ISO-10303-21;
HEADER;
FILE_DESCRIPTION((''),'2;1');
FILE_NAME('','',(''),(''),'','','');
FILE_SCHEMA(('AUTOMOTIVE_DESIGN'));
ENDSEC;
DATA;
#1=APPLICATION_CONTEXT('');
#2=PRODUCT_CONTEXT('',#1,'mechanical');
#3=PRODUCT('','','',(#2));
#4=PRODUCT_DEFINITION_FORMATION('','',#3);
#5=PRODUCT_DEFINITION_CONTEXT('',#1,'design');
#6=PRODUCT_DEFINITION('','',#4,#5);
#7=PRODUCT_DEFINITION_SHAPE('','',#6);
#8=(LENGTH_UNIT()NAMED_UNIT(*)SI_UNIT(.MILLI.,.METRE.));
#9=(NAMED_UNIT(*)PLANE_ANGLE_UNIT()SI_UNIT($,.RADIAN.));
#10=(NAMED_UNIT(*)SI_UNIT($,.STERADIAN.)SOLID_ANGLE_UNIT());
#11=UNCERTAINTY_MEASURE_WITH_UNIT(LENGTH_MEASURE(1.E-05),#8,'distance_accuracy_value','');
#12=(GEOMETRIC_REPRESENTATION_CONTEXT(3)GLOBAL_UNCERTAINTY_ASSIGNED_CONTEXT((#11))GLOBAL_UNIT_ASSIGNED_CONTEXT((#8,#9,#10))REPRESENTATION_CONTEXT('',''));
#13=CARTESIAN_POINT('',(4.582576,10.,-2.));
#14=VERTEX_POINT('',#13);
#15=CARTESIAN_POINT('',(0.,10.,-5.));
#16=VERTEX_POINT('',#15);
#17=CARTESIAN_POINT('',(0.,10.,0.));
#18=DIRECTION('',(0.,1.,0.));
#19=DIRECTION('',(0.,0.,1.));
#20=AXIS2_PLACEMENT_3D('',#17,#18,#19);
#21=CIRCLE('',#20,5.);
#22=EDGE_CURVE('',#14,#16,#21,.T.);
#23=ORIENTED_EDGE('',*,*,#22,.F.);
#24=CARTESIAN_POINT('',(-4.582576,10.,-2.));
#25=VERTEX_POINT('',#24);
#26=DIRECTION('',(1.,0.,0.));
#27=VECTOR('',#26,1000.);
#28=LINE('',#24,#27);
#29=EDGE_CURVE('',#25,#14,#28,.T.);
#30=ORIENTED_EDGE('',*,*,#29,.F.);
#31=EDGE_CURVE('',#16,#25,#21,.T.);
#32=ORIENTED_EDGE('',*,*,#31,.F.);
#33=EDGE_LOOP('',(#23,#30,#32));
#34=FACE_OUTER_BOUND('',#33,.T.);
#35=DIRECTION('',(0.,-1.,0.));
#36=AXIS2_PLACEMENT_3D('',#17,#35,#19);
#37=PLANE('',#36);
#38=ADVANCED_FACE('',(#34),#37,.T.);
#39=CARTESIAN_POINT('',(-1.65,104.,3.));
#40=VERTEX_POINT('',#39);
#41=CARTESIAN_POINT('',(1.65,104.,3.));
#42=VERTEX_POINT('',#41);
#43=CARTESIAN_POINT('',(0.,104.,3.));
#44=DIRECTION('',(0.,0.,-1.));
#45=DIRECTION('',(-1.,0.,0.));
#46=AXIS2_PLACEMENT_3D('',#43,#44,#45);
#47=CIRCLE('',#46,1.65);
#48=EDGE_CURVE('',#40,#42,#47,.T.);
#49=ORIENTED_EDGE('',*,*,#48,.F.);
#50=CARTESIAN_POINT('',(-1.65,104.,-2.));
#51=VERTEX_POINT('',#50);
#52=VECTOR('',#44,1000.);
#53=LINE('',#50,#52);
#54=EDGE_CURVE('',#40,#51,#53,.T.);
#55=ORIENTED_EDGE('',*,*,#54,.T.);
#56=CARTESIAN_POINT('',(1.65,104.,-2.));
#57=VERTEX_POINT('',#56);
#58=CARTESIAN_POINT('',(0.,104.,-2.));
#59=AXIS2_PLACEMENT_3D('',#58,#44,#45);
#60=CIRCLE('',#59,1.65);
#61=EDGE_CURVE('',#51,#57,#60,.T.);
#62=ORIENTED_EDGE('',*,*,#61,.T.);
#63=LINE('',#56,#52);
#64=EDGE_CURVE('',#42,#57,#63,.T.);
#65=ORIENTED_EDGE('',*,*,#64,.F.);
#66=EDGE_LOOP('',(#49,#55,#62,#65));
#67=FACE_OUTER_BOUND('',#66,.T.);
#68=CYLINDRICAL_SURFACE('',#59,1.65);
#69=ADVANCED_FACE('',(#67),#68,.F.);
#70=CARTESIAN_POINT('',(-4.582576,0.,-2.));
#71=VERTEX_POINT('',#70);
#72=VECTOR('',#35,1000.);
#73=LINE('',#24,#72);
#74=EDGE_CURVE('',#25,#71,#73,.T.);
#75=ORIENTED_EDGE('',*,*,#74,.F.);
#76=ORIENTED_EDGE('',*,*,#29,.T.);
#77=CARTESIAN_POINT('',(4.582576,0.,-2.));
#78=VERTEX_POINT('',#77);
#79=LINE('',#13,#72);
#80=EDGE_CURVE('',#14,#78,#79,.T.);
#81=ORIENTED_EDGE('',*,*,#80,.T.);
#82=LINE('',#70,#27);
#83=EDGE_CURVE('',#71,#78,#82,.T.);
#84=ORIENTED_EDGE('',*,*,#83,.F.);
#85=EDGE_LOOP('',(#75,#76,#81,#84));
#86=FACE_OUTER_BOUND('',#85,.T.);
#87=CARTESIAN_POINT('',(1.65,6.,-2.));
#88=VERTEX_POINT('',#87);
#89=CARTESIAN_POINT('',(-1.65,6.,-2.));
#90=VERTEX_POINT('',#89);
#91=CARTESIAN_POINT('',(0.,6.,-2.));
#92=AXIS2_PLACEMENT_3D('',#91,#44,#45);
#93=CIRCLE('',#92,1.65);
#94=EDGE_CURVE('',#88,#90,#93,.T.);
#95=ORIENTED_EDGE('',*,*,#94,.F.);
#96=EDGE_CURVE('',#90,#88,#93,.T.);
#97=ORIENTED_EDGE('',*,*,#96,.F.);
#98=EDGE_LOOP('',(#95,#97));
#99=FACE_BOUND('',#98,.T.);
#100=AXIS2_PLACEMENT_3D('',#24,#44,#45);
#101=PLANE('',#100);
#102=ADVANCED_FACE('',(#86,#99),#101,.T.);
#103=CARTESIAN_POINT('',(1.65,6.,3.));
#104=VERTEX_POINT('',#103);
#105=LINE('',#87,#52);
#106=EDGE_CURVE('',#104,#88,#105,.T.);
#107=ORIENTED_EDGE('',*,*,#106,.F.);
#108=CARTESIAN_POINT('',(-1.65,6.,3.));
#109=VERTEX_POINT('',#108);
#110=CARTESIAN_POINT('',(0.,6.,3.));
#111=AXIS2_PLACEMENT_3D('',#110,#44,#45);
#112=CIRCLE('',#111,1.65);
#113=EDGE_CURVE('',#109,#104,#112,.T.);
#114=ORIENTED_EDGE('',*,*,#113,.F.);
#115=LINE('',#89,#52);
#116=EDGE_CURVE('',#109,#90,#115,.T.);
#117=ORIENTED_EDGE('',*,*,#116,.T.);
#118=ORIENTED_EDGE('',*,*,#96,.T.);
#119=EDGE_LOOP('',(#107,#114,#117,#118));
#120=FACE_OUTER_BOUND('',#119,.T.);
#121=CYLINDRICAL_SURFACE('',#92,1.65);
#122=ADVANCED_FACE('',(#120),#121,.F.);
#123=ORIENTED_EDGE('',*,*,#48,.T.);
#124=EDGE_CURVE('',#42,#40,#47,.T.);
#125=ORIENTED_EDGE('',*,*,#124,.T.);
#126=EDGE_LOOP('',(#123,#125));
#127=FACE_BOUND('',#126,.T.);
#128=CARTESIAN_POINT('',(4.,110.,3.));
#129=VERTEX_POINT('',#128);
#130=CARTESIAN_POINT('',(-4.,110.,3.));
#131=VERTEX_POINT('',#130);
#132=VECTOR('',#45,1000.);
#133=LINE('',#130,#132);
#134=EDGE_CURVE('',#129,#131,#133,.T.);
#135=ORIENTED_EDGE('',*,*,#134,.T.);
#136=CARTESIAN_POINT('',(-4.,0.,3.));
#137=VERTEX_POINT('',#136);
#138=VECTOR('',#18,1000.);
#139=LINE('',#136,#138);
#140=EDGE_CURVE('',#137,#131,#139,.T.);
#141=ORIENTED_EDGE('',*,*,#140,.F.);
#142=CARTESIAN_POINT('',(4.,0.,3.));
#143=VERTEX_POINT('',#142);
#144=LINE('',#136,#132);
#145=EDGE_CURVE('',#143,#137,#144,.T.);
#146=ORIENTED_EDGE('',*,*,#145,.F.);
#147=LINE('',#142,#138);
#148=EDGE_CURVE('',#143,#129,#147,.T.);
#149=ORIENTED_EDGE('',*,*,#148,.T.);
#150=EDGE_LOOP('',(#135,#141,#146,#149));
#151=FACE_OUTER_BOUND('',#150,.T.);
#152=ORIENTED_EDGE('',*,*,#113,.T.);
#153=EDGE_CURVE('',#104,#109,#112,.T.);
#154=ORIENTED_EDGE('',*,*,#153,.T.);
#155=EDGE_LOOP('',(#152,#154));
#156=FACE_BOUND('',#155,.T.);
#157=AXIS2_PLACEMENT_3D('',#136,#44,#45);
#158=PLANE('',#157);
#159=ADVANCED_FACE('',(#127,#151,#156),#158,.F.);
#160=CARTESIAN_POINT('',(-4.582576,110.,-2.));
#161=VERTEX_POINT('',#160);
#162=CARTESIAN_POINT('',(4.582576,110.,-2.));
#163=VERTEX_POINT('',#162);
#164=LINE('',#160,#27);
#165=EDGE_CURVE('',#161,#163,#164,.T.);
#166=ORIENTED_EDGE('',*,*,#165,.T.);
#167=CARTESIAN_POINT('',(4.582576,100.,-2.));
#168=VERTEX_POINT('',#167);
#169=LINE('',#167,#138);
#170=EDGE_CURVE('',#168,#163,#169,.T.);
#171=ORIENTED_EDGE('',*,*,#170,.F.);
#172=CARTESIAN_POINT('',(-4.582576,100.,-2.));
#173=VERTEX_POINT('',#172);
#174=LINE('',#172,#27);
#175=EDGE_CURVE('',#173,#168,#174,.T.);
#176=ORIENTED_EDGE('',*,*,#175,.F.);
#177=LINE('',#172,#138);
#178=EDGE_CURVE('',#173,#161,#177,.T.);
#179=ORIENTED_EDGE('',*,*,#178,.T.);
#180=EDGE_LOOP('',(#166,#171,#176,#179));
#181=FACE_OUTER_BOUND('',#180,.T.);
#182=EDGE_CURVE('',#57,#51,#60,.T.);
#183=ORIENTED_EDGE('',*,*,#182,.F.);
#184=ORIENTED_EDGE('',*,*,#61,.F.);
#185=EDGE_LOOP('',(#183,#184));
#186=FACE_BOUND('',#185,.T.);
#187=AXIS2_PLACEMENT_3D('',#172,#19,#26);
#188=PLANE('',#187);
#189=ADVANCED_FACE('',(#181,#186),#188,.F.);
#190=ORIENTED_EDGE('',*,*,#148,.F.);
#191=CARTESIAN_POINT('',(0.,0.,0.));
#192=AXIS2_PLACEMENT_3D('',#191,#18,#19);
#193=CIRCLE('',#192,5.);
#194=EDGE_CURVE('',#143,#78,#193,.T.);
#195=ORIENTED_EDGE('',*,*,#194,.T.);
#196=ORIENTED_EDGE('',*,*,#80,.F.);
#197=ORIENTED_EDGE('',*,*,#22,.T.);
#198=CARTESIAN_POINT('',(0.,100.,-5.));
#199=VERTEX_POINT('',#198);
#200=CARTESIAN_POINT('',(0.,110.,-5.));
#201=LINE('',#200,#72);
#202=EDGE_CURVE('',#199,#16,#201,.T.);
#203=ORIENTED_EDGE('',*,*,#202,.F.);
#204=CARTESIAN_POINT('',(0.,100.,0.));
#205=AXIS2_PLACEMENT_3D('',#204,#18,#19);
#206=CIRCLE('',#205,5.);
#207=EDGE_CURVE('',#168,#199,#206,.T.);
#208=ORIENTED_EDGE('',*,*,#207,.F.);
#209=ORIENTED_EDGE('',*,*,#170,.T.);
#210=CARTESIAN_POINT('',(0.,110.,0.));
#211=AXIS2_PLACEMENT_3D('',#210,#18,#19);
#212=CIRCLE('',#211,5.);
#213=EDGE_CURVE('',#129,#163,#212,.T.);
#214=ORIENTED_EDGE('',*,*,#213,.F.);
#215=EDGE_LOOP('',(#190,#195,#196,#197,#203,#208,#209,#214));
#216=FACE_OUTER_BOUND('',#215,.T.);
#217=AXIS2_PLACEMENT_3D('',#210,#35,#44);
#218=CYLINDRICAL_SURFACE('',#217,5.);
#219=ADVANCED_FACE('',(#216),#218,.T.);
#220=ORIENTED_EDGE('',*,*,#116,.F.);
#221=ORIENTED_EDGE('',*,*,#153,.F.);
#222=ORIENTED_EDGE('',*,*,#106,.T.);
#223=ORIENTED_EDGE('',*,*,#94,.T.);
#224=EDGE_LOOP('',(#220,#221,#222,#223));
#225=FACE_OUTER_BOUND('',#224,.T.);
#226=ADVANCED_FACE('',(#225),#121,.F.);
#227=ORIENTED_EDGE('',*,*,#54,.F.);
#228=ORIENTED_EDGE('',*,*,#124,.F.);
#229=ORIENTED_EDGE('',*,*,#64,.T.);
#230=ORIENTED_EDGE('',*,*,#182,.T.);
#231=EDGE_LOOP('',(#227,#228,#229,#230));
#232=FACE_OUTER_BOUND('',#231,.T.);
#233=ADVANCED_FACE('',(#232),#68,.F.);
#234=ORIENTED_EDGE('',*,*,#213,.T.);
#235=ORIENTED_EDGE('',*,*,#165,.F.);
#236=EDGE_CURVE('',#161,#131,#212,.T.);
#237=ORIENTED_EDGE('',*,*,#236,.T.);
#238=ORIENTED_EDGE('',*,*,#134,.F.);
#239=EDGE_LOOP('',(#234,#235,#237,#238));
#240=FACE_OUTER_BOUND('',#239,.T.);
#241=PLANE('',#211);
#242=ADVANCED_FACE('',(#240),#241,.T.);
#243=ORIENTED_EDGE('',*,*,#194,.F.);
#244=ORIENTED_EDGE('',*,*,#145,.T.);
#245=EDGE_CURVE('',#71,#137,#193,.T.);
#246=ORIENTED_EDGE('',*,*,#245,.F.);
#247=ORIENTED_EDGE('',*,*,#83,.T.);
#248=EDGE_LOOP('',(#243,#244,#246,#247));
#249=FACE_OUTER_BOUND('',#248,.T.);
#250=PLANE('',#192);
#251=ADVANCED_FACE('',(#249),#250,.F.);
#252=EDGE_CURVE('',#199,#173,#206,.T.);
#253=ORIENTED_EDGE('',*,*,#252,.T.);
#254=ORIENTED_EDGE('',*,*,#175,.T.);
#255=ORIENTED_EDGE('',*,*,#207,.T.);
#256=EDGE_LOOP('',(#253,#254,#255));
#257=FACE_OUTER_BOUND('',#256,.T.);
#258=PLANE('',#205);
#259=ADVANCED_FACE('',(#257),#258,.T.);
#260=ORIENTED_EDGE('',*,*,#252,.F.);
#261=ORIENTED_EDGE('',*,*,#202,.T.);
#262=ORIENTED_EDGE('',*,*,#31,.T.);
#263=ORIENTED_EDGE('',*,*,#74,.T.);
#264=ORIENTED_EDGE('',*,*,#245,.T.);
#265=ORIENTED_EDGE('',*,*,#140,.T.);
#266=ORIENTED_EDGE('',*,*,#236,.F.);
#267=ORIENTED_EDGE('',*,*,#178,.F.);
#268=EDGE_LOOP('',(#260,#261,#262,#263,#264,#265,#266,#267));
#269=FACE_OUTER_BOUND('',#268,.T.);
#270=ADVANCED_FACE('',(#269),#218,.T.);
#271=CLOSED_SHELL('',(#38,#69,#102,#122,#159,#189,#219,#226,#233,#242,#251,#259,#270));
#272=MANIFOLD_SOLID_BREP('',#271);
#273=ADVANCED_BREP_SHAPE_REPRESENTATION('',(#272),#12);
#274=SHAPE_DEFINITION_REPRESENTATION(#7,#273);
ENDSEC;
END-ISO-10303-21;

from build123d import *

# Parameters (mm, degrees)
SKETCH1_R           = 5
BOSS_EXTRUDE1_DEPTH = 110
CUT_EXTRUDE1_DEPTH  = 111.227038425
CUT_EXTRUDE2_START  = -10
CUT_EXTRUDE2_DEPTH  = 10
M4_TAPPED_HOLE2_D   = 3.3


with BuildPart() as part:
    # Sketch1 → Boss-Extrude1 (new body)
    with BuildSketch(Plane(origin=(0, 0, 0), x_dir=(1, 0, 0), z_dir=(0, 1, 0))):
        with Locations(Location((0, 0, 0), (0, 0, 270))):
            Circle(SKETCH1_R)
    extrude(amount=BOSS_EXTRUDE1_DEPTH)

    # Sketch2 → Cut-Extrude1 (cut, through all)
    with BuildSketch(Plane(origin=(0, 110, 0), x_dir=(1, 0, 0), z_dir=(0, 1, 0))):
        with BuildLine():
            Line((-4, -3), (4, -3))
            ThreePointArc((4, -3), (0, -5), (-4, -3))
        make_face()
    extrude(amount=-CUT_EXTRUDE1_DEPTH, mode=Mode.SUBTRACT)

    # Sketch3 → Cut-Extrude2 (cut)
    with BuildSketch(Plane(origin=(0, 110, 0), x_dir=(1, 0, 0), z_dir=(0, 1, 0)).offset(CUT_EXTRUDE2_START)):
        with BuildLine():
            Line((-4.582575695, 2), (4.582575695, 2))
            ThreePointArc((4.582575695, 2), (0, 5), (-4.582575695, 2))
        make_face()
    cut_extrude2 = extrude(amount=CUT_EXTRUDE2_DEPTH, mode=Mode.SUBTRACT)

    # Mirror1: Cut-Extrude2 across plane
    add(cut_extrude2.mirror(Plane.ZX.offset(55)), mode=Mode.SUBTRACT)

    # M4 Tapped Hole2 (through all)
    with Locations(Plane(origin=(0, 0, -2), x_dir=(-1, 0, 0), z_dir=(0, 0, -1))):
        with Locations((0, 104), (0, 6)):
            Hole(M4_TAPPED_HOLE2_D / 2)


solid = part.part
